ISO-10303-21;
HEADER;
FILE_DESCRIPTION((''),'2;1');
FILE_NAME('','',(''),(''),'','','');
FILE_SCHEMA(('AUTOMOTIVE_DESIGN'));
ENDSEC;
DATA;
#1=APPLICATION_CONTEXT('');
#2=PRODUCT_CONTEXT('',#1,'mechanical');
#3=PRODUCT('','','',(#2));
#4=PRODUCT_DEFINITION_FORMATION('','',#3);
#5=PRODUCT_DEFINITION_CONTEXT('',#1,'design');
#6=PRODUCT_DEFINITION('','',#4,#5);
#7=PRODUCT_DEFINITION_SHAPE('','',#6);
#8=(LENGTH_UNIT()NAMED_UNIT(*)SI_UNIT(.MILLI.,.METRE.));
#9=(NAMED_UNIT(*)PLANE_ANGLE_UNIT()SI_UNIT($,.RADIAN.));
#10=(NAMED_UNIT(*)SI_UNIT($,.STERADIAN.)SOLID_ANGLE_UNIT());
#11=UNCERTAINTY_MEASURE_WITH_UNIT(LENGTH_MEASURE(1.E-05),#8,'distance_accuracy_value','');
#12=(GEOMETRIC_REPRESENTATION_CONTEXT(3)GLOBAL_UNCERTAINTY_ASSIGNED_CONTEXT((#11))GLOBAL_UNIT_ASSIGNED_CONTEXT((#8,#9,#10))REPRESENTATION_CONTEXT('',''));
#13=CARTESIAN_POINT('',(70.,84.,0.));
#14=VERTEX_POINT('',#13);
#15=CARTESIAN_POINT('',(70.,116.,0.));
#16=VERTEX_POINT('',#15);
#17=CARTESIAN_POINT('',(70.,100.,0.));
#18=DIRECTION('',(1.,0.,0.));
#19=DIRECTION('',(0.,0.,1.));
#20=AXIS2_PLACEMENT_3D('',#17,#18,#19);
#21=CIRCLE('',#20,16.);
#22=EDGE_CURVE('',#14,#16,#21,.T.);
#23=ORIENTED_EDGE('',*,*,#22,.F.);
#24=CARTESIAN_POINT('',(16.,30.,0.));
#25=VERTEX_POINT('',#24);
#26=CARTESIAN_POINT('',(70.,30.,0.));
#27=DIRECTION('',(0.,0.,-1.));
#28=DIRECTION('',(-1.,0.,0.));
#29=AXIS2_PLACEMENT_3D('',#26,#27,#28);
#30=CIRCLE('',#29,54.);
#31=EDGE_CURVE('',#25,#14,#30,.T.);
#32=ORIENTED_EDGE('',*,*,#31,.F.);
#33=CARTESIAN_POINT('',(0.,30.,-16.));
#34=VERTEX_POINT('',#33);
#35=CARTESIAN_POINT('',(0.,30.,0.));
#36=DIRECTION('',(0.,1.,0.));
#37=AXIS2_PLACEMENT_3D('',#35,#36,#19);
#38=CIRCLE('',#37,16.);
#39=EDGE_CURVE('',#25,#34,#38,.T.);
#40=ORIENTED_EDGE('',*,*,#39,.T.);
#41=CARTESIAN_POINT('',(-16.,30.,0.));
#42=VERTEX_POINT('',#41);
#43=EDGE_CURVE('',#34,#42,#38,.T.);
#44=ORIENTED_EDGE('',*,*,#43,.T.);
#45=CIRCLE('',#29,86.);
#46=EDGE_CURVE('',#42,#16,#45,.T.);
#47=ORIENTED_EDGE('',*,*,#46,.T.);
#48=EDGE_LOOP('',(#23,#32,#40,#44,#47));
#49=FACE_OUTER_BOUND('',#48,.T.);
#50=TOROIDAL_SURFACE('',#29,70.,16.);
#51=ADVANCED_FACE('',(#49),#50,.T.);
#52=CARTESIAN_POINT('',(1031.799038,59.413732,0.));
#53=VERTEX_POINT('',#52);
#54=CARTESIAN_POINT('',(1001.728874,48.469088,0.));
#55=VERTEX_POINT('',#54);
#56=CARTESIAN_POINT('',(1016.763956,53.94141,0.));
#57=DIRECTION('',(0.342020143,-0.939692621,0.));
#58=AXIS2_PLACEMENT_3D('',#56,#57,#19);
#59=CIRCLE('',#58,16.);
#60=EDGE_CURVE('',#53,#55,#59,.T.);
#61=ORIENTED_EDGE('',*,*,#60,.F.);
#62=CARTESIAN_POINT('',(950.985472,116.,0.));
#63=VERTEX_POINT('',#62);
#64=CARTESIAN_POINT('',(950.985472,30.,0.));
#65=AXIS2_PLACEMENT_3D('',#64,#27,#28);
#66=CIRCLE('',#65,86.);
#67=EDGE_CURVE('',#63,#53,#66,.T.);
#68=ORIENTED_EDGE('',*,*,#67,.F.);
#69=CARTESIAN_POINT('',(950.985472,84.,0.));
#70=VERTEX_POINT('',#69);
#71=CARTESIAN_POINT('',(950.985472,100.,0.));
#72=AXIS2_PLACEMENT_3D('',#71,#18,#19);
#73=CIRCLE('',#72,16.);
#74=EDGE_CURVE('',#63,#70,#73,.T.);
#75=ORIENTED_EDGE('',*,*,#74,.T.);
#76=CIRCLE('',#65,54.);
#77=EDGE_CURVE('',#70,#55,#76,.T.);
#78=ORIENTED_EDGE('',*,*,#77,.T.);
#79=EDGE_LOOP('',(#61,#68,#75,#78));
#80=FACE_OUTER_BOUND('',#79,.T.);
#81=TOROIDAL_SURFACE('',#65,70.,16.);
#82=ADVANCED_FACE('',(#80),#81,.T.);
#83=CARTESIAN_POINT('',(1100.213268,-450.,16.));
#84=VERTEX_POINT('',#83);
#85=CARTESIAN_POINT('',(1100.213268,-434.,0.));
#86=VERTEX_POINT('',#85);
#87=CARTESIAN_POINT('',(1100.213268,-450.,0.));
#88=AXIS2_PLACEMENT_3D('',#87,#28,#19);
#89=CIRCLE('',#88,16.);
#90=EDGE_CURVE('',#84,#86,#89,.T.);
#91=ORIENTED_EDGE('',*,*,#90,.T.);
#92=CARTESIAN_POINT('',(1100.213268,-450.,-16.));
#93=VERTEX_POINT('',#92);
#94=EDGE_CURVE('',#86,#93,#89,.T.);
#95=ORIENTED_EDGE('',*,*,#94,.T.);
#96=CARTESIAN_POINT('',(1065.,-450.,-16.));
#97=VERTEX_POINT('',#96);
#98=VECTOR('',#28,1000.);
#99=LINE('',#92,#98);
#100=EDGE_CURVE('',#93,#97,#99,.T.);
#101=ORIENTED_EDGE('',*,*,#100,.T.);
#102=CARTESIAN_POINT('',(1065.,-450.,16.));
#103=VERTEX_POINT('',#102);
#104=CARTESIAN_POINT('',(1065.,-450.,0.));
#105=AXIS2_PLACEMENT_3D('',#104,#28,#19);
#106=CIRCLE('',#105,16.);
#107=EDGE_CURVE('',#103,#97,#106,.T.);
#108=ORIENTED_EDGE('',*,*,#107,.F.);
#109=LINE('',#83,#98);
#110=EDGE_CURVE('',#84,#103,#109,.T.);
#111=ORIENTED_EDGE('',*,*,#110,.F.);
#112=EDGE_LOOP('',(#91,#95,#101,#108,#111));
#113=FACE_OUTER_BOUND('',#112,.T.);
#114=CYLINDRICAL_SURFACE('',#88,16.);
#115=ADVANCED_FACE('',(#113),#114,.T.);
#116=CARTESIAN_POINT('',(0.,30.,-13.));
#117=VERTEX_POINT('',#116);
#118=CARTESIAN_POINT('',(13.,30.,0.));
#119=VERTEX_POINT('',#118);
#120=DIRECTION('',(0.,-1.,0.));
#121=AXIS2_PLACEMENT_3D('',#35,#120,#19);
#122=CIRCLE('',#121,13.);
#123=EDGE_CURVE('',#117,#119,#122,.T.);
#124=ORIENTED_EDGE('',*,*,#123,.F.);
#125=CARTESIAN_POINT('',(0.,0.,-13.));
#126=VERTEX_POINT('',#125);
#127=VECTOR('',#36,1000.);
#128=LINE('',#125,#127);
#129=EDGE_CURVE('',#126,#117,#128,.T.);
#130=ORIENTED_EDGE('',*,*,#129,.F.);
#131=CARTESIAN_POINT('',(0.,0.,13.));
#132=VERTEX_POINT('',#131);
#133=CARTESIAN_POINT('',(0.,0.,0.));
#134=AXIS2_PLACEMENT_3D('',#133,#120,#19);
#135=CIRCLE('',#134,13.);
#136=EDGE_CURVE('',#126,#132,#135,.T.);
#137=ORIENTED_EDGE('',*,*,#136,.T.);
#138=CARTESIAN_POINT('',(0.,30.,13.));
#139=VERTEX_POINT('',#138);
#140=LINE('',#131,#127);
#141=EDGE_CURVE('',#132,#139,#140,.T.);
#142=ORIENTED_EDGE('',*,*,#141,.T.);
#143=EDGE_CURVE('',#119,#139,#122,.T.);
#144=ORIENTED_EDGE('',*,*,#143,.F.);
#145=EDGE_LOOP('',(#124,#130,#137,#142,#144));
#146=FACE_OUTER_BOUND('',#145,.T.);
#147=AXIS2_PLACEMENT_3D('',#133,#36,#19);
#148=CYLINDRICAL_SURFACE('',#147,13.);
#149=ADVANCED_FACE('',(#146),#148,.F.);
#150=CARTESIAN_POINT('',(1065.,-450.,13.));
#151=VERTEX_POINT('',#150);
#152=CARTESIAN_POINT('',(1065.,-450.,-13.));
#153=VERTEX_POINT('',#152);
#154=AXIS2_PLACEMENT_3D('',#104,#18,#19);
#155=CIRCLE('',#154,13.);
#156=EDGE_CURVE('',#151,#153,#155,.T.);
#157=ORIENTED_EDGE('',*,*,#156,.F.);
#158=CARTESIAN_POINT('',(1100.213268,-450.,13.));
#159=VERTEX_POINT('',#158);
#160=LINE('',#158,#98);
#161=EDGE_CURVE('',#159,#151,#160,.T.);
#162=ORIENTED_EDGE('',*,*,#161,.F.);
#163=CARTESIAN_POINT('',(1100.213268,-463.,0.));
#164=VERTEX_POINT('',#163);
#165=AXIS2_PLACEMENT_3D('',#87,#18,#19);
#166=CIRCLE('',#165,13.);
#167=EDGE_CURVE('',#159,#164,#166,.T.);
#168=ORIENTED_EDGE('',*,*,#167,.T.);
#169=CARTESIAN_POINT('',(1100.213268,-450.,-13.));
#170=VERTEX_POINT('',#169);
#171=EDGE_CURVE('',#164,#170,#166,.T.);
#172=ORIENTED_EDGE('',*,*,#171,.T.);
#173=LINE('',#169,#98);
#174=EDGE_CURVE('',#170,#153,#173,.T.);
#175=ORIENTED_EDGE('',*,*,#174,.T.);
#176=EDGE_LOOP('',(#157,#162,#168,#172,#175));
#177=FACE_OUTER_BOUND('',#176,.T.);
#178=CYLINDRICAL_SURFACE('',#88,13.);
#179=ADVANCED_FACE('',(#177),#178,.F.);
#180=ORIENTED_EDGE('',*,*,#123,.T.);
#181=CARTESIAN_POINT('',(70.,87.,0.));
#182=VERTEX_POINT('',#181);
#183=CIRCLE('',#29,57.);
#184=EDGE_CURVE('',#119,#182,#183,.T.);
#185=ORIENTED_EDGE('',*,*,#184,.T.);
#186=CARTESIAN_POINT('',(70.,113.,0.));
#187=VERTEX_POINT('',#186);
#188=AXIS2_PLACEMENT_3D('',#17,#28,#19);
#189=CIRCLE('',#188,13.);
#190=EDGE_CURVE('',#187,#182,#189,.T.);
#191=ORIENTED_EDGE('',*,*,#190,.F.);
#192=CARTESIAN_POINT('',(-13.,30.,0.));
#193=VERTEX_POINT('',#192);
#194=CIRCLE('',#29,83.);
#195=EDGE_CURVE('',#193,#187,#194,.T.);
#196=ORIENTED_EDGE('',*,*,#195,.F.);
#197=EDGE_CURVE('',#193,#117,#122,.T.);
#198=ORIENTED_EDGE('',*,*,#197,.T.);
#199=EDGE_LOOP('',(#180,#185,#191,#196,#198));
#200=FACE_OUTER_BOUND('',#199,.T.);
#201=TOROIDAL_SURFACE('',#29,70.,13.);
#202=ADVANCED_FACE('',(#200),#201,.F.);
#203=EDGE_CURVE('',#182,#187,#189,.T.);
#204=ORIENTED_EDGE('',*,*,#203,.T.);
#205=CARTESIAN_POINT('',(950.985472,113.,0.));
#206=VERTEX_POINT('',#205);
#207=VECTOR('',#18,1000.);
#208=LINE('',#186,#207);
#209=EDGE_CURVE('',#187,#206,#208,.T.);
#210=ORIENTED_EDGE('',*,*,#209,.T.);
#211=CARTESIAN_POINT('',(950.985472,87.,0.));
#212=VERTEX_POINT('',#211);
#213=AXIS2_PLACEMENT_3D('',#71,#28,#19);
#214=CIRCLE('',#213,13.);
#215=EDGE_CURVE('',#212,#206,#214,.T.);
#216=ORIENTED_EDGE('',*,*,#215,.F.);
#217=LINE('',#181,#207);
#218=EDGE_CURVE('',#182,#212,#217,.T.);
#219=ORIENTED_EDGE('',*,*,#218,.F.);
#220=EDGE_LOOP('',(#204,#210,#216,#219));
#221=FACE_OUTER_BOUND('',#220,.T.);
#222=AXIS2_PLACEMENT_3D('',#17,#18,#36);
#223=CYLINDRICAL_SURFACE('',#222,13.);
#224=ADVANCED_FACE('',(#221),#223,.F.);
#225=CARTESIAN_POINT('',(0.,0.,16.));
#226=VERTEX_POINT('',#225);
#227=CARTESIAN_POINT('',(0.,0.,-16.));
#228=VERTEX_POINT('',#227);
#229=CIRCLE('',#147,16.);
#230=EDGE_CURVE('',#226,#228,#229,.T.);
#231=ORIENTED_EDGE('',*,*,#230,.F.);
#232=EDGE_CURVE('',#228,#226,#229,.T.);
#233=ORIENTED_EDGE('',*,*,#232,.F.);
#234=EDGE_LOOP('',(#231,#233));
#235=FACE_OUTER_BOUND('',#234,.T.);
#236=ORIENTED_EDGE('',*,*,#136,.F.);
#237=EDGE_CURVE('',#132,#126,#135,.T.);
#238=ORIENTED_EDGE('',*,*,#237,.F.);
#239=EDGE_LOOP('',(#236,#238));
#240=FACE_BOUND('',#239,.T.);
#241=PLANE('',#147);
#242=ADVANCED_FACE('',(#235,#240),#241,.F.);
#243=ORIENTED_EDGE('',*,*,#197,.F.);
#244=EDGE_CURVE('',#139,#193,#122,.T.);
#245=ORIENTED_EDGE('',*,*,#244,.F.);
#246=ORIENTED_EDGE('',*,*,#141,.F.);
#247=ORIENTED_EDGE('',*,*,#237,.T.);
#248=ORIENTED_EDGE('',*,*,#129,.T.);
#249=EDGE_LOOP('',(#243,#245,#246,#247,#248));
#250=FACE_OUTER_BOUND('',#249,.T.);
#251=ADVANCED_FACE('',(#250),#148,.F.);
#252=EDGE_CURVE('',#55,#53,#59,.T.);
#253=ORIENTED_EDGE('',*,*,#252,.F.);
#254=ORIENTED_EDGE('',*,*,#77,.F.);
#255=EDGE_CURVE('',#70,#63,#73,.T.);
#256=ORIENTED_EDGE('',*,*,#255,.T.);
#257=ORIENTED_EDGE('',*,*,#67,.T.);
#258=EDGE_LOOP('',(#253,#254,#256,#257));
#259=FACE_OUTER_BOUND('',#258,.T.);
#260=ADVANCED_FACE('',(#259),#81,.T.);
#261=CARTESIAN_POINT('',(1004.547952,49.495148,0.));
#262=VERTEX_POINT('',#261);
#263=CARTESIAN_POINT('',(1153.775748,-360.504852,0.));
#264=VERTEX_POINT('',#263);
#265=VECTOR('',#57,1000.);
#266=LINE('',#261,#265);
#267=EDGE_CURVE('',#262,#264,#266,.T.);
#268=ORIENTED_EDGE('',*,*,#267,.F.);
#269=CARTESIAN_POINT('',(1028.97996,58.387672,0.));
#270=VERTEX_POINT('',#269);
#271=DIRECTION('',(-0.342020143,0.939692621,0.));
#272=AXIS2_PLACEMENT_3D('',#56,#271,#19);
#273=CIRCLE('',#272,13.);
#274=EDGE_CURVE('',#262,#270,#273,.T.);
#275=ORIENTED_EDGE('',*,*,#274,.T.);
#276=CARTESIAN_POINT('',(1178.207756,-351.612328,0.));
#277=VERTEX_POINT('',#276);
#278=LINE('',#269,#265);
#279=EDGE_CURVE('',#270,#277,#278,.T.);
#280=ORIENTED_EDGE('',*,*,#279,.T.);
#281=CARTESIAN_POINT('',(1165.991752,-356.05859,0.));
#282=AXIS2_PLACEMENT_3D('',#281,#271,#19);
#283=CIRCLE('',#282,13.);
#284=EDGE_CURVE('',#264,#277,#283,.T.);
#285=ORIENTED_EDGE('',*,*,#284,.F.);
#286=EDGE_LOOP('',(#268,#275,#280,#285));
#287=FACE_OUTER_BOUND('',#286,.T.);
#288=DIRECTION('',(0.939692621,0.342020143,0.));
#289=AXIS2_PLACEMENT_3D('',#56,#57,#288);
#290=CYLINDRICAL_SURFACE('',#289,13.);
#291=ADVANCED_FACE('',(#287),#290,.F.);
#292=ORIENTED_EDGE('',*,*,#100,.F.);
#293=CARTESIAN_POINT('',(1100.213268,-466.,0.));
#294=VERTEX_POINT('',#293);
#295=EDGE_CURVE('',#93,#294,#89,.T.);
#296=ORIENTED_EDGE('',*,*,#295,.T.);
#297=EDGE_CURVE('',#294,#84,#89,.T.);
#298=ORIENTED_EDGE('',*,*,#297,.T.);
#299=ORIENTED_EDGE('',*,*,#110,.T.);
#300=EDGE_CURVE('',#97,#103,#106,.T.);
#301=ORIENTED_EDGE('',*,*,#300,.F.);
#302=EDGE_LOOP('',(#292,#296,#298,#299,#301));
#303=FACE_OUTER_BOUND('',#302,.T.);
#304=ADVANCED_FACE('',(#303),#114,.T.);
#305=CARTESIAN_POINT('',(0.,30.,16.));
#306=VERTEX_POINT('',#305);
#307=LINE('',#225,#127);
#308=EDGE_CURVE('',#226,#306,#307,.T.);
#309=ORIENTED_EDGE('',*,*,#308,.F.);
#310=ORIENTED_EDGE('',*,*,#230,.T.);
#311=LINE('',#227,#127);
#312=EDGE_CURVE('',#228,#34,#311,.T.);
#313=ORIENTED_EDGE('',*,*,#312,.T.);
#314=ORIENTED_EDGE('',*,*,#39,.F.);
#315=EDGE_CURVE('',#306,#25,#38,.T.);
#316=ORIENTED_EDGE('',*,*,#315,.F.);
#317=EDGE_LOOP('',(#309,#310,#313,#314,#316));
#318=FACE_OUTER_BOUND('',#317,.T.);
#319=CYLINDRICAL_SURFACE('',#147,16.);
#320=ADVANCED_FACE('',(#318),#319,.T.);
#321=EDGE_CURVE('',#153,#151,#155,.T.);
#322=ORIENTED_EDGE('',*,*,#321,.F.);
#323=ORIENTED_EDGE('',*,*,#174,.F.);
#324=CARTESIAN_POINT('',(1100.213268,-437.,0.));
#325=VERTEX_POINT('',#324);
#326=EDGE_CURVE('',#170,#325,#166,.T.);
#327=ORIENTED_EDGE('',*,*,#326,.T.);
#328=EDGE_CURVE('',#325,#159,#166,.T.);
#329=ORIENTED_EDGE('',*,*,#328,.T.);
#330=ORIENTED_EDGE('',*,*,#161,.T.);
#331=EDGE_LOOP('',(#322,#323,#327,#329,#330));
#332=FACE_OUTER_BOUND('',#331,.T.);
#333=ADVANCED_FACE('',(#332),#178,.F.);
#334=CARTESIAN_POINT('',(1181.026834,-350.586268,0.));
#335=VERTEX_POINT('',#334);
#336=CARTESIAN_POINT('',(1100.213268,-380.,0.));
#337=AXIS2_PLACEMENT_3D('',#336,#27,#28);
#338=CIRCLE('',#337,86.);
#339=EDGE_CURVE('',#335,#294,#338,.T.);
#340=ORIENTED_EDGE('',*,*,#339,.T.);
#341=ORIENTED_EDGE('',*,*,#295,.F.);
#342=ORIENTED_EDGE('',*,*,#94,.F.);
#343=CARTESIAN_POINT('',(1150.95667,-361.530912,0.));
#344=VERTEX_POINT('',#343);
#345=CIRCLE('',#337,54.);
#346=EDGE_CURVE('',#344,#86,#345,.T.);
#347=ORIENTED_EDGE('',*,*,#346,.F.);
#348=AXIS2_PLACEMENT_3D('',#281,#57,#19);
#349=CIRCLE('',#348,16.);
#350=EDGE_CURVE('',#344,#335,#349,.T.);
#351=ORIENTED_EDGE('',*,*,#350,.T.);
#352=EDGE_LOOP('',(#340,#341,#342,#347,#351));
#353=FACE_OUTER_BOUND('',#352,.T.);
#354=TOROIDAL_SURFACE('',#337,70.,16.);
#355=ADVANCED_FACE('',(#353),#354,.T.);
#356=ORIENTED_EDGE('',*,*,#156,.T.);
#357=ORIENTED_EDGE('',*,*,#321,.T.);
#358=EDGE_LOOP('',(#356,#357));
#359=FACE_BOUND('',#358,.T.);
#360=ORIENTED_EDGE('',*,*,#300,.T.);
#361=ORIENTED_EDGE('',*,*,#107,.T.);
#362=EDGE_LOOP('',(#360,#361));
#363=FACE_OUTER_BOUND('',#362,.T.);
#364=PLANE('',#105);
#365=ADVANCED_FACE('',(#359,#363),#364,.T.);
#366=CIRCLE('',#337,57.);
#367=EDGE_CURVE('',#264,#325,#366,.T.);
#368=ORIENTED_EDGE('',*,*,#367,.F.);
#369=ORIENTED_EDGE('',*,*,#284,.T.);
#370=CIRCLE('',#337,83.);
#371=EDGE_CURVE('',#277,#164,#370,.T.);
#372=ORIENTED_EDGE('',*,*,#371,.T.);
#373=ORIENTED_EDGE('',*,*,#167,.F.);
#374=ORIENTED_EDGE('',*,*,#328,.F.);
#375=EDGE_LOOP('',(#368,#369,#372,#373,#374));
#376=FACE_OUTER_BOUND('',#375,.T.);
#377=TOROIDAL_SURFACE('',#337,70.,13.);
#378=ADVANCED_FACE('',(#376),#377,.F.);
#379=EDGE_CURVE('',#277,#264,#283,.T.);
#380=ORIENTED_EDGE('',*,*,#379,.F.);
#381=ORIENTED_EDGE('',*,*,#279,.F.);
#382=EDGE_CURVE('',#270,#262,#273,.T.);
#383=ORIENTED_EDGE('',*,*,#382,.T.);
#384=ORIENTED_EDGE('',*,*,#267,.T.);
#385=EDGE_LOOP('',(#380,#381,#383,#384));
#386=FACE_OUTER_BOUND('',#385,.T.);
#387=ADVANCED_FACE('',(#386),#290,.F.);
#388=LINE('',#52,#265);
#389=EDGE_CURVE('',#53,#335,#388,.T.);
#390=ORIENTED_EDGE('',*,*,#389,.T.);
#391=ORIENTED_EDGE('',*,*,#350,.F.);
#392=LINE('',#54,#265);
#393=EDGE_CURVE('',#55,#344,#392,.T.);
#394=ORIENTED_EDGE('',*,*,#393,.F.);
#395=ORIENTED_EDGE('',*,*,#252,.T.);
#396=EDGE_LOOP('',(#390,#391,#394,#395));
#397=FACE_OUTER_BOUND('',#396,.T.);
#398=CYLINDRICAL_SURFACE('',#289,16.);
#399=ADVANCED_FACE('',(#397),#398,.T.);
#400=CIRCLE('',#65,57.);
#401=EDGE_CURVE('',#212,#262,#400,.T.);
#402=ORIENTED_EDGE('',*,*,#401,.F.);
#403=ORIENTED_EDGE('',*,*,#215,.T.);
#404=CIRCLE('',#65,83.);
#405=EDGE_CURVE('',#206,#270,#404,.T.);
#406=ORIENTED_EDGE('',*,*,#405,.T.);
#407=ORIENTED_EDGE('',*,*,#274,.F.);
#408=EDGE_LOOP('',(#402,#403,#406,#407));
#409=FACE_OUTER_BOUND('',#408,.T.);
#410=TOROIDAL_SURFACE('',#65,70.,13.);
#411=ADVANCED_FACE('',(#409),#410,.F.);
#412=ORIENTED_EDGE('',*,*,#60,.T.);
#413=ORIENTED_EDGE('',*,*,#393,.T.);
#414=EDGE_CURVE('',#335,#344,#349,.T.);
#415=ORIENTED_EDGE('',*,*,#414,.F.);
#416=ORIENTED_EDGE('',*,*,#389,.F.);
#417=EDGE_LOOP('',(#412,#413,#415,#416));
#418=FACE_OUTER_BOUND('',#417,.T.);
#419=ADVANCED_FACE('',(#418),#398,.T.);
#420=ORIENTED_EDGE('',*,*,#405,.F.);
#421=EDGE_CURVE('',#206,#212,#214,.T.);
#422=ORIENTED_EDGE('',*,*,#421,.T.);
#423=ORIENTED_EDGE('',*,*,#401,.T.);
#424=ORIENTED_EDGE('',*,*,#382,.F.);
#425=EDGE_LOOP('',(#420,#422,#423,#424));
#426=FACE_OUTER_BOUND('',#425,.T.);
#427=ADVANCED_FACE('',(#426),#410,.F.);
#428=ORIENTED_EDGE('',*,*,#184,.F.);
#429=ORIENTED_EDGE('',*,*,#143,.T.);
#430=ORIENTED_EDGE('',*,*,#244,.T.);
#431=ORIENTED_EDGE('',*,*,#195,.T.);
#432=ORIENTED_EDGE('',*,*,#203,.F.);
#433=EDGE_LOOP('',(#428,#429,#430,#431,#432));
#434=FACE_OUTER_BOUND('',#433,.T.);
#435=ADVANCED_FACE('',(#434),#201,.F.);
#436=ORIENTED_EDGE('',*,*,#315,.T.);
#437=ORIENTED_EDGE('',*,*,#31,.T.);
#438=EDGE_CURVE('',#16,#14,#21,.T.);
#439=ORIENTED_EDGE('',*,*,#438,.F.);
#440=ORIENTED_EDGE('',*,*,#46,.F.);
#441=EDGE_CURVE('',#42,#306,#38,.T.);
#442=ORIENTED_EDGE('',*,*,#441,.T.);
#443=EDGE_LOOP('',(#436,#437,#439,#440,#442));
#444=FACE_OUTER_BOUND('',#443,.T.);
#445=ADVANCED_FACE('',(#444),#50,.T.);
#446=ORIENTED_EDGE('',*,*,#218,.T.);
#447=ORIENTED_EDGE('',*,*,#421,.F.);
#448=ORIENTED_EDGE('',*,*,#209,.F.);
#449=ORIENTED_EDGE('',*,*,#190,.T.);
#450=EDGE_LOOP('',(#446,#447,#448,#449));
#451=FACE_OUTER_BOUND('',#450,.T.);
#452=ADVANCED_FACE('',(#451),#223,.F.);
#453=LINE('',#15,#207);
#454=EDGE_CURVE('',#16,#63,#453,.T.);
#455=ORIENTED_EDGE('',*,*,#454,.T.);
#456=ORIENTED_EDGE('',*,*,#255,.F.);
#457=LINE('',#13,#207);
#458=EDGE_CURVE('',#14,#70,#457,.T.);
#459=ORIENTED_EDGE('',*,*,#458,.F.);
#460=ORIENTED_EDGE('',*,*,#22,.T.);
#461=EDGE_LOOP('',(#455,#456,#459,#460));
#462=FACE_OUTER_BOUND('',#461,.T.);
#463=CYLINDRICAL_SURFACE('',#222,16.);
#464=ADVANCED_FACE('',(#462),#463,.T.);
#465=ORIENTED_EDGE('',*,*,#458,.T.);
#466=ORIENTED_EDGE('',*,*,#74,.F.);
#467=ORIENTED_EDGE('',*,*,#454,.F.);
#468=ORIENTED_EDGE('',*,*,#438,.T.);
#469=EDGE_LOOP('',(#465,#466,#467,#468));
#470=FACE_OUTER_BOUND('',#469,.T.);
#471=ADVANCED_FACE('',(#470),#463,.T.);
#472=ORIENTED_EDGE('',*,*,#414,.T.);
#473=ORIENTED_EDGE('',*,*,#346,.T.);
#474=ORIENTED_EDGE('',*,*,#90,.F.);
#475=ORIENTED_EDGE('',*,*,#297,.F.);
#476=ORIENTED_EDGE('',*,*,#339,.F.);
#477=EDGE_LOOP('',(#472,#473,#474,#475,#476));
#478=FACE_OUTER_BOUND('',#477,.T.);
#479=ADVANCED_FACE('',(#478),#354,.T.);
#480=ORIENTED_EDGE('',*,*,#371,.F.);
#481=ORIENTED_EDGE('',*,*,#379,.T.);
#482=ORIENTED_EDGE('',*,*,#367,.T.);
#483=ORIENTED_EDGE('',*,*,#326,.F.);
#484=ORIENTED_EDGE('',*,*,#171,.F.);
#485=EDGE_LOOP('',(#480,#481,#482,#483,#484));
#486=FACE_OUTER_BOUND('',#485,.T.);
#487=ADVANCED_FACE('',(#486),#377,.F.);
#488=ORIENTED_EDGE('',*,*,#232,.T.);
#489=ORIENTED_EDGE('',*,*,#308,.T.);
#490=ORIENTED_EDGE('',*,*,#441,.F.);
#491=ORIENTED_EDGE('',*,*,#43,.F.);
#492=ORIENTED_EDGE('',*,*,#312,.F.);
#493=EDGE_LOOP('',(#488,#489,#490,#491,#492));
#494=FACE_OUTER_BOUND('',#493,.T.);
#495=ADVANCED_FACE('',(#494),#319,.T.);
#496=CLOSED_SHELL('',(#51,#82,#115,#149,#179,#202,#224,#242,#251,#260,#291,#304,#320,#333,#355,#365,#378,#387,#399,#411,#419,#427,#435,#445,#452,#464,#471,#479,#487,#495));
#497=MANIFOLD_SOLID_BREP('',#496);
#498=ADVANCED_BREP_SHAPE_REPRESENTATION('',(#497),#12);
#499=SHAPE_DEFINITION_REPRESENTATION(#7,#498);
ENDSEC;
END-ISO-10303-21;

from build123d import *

# Parameters (mm, degrees)
SKETCH2_R   = 16
SKETCH2_R_2 = 13


with BuildPart() as part:
    # Sweep1: sweep along a path in Sketch1
    with BuildLine(Plane.XY) as sweep1_path:
        Line((0, 0), (0, 30))
        ThreePointArc((0, 30), (20.502525317, 79.497474683), (70, 100))
        Line((70, 100), (950.985472325, 100))
        ThreePointArc((950.985472325, 100), (991.13582287, 87.3406431), (1016.76395578, 53.941410033))
        Line((1016.76395578, 53.941410033), (1165.991751829, -356.058589967))
        ThreePointArc((1165.991751829, -356.058589967), (1157.553911475, -420.150350545), (1100.213268374, -450))
        Line((1100.213268374, -450), (1065, -450))
    # Sketch2 → Sweep1 (sweep)
    with BuildSketch(Plane(origin=(0, 0, 0), x_dir=(1, 0, 0), z_dir=(0, 1, 0))):
        Circle(SKETCH2_R)
        Circle(SKETCH2_R_2, mode=Mode.SUBTRACT)
    sweep(path=sweep1_path.line)


solid = part.part
